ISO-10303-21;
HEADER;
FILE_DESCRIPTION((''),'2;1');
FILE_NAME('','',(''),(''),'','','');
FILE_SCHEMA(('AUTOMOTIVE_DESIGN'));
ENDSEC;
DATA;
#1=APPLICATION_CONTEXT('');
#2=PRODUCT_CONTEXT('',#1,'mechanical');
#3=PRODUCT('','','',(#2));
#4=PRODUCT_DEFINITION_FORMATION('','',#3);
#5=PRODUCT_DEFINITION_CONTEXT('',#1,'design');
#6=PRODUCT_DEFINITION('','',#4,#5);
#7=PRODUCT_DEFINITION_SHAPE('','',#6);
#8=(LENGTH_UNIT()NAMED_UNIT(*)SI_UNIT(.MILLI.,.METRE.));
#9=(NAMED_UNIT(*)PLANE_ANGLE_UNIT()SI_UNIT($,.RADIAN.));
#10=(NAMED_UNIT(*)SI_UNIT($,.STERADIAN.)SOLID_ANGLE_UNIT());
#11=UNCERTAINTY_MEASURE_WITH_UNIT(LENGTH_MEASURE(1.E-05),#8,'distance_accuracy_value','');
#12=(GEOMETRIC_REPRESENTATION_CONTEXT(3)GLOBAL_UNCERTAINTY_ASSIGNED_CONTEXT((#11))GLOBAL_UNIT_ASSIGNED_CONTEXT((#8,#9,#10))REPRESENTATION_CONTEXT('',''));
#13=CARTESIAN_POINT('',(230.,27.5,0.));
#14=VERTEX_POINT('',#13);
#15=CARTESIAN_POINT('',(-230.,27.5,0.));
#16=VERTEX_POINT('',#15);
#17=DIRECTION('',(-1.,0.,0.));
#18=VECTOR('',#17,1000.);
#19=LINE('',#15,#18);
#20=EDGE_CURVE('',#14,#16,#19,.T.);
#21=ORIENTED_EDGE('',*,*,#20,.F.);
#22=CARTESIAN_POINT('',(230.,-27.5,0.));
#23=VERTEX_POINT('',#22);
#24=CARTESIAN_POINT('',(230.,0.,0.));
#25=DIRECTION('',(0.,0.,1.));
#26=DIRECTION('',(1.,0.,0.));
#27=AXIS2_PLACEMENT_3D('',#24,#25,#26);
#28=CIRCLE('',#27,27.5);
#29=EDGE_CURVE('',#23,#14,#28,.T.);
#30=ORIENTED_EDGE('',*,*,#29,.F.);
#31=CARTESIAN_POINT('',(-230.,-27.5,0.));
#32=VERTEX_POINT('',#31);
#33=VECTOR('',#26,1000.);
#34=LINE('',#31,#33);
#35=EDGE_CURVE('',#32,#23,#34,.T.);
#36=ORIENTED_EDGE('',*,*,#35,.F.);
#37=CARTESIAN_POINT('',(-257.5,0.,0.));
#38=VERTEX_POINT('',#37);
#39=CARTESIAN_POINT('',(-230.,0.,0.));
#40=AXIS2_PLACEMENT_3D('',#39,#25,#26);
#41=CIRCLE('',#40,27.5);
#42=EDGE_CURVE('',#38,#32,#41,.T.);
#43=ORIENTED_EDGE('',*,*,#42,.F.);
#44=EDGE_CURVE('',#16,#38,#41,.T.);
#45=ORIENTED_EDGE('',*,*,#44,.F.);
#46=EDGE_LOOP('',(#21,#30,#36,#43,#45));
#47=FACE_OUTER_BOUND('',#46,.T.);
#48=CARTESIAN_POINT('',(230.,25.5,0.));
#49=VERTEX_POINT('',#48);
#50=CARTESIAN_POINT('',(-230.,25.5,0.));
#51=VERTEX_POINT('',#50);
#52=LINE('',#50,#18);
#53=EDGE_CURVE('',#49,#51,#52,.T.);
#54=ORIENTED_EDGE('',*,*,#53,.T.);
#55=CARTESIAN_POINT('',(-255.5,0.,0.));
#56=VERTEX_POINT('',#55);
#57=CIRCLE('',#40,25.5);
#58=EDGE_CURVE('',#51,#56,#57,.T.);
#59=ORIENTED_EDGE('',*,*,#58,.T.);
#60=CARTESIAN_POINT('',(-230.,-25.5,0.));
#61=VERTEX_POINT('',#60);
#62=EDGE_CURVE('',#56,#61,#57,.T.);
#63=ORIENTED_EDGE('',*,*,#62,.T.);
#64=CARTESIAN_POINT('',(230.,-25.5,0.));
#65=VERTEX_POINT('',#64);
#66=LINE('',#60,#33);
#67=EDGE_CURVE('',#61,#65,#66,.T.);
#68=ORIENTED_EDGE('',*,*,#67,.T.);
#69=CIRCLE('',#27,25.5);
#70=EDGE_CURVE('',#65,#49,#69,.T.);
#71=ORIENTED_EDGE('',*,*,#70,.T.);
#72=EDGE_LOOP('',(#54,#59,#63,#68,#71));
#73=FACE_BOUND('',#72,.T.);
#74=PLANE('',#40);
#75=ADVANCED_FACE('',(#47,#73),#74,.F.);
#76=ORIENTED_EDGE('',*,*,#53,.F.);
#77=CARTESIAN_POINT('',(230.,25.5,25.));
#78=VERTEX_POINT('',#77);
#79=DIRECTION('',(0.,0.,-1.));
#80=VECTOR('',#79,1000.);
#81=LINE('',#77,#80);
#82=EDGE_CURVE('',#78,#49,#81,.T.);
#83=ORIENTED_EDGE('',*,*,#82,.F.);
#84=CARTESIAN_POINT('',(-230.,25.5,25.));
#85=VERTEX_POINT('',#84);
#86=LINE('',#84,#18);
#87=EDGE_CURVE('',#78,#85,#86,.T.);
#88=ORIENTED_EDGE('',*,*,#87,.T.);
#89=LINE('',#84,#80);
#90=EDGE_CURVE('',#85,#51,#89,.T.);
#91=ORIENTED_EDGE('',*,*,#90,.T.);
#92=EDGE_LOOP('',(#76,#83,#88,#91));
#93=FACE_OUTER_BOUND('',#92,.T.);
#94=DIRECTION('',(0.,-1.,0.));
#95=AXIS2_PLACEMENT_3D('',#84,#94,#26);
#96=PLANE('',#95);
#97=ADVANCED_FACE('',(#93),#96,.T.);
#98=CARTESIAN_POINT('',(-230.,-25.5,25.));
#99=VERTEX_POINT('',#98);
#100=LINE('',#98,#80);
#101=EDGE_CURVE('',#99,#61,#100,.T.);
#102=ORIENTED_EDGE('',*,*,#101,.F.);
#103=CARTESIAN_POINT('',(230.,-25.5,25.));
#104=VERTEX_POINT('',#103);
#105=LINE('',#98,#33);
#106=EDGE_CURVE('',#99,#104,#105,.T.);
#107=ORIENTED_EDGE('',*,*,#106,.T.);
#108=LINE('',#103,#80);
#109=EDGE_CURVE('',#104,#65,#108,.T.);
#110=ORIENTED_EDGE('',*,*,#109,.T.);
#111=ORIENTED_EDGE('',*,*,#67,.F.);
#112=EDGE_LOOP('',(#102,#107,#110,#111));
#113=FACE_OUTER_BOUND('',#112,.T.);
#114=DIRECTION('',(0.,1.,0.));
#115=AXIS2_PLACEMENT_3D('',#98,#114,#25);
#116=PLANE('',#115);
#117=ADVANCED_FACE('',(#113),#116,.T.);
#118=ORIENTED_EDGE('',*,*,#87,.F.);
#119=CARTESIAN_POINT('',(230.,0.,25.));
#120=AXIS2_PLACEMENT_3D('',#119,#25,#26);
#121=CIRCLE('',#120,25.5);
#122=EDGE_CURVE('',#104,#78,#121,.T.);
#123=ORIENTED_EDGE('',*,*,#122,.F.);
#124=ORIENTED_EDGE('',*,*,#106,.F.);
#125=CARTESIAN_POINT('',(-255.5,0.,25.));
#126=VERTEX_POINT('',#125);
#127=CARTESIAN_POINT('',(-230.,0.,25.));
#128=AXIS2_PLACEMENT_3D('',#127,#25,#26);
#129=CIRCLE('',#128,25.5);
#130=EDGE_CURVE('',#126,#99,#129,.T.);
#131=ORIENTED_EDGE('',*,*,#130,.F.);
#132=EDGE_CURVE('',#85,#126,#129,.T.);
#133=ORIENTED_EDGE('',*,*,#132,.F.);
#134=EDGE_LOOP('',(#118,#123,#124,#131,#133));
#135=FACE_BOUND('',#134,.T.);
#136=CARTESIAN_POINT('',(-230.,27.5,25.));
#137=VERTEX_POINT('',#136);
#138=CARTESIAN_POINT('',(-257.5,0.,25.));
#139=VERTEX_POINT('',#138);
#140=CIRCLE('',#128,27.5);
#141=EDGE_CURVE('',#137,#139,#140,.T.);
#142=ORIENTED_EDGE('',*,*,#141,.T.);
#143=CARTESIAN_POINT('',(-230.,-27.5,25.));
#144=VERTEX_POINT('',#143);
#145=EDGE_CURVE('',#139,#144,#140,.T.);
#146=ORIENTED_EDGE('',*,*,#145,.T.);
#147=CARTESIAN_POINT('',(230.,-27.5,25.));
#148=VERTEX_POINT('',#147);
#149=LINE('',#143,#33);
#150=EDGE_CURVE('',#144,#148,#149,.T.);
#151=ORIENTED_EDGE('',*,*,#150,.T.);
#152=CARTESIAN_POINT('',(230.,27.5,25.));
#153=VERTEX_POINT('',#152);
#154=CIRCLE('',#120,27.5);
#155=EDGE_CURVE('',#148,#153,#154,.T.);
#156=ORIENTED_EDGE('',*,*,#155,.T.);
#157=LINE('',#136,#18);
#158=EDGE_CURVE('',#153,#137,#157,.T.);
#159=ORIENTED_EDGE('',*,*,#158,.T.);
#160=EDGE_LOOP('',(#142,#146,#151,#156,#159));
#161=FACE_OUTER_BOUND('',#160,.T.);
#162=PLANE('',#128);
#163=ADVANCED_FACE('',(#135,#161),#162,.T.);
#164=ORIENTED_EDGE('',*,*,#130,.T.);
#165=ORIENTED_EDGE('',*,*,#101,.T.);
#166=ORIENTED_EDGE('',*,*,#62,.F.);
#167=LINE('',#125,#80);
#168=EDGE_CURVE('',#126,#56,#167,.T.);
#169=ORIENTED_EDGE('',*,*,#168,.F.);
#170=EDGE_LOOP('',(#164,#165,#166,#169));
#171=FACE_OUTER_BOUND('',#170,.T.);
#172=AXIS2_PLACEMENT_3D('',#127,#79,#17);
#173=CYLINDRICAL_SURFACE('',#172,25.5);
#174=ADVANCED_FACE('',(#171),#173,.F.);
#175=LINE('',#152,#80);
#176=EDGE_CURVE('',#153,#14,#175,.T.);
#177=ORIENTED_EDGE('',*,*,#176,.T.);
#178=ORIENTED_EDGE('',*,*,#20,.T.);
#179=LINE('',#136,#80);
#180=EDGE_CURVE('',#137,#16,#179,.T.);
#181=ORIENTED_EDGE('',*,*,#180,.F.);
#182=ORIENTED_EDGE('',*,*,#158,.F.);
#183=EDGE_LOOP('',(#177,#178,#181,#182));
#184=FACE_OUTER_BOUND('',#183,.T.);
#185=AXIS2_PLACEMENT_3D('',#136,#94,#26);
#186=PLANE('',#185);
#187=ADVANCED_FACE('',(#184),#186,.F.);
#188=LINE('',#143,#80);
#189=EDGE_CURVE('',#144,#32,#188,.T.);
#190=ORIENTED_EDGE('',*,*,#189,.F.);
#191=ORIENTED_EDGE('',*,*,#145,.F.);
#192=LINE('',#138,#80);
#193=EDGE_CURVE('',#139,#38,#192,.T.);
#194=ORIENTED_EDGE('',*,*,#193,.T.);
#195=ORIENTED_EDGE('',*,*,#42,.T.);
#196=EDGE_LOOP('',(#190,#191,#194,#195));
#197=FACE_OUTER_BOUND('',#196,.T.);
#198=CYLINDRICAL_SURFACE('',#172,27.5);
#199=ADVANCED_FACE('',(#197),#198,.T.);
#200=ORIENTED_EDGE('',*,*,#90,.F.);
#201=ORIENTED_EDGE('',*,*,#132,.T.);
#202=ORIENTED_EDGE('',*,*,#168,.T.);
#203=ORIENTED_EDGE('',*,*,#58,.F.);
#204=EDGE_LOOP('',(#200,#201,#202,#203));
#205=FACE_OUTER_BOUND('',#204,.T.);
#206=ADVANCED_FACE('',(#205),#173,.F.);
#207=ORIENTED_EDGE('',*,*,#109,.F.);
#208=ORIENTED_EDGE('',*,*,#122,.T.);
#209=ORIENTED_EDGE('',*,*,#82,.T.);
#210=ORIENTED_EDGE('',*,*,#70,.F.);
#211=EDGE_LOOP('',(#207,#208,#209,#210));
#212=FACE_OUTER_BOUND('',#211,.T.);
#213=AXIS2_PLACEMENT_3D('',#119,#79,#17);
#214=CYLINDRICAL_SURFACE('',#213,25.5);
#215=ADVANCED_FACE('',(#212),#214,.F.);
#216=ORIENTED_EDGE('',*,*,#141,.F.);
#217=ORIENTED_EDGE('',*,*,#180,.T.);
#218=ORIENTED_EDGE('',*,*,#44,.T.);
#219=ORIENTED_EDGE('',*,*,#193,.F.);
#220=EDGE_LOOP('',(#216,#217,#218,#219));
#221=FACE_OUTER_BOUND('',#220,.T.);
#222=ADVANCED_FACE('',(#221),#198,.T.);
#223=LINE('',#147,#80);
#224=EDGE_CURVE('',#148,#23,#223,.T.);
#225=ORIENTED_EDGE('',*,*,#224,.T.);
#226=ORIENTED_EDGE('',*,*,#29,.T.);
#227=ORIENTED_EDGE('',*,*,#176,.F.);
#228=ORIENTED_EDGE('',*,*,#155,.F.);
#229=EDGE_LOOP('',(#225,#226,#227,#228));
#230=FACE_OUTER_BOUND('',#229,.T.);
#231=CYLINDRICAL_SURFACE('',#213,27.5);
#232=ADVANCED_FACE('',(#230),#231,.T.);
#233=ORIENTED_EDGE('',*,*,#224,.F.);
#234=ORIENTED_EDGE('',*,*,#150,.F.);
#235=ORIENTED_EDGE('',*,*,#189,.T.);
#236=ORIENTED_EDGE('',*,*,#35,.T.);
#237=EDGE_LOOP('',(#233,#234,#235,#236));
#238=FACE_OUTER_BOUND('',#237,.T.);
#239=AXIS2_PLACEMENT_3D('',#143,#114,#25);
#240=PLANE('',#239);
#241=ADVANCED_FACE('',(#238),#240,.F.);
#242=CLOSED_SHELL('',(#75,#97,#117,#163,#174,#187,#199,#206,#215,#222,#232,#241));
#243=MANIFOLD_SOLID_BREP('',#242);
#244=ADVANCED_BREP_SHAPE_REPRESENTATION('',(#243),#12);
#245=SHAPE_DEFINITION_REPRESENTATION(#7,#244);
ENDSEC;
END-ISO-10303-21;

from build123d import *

# Parameters (mm, degrees)
EXTRUDE_1_DEPTH = 25


with BuildPart() as part:
    # 草图1 → 拉伸-薄壁1 (new body)
    with BuildSketch(Plane.XY):
        with BuildLine():
            Line((230, -27.5), (-230, -27.5))
            ThreePointArc((-230, -27.5), (-257.5, 0), (-230, 27.5))
            Line((-230, 27.5), (230, 27.5))
            ThreePointArc((230, 27.5), (257.5, 0), (230, -27.5))
        make_face()
        with BuildLine():
            Line((230, -25.5), (-230, -25.5))
            ThreePointArc((-230, -25.5), (-255.5, 0), (-230, 25.5))
            Line((-230, 25.5), (230, 25.5))
            ThreePointArc((230, 25.5), (255.5, 0), (230, -25.5))
        make_face(mode=Mode.SUBTRACT)
    extrude(amount=EXTRUDE_1_DEPTH)


solid = part.part
